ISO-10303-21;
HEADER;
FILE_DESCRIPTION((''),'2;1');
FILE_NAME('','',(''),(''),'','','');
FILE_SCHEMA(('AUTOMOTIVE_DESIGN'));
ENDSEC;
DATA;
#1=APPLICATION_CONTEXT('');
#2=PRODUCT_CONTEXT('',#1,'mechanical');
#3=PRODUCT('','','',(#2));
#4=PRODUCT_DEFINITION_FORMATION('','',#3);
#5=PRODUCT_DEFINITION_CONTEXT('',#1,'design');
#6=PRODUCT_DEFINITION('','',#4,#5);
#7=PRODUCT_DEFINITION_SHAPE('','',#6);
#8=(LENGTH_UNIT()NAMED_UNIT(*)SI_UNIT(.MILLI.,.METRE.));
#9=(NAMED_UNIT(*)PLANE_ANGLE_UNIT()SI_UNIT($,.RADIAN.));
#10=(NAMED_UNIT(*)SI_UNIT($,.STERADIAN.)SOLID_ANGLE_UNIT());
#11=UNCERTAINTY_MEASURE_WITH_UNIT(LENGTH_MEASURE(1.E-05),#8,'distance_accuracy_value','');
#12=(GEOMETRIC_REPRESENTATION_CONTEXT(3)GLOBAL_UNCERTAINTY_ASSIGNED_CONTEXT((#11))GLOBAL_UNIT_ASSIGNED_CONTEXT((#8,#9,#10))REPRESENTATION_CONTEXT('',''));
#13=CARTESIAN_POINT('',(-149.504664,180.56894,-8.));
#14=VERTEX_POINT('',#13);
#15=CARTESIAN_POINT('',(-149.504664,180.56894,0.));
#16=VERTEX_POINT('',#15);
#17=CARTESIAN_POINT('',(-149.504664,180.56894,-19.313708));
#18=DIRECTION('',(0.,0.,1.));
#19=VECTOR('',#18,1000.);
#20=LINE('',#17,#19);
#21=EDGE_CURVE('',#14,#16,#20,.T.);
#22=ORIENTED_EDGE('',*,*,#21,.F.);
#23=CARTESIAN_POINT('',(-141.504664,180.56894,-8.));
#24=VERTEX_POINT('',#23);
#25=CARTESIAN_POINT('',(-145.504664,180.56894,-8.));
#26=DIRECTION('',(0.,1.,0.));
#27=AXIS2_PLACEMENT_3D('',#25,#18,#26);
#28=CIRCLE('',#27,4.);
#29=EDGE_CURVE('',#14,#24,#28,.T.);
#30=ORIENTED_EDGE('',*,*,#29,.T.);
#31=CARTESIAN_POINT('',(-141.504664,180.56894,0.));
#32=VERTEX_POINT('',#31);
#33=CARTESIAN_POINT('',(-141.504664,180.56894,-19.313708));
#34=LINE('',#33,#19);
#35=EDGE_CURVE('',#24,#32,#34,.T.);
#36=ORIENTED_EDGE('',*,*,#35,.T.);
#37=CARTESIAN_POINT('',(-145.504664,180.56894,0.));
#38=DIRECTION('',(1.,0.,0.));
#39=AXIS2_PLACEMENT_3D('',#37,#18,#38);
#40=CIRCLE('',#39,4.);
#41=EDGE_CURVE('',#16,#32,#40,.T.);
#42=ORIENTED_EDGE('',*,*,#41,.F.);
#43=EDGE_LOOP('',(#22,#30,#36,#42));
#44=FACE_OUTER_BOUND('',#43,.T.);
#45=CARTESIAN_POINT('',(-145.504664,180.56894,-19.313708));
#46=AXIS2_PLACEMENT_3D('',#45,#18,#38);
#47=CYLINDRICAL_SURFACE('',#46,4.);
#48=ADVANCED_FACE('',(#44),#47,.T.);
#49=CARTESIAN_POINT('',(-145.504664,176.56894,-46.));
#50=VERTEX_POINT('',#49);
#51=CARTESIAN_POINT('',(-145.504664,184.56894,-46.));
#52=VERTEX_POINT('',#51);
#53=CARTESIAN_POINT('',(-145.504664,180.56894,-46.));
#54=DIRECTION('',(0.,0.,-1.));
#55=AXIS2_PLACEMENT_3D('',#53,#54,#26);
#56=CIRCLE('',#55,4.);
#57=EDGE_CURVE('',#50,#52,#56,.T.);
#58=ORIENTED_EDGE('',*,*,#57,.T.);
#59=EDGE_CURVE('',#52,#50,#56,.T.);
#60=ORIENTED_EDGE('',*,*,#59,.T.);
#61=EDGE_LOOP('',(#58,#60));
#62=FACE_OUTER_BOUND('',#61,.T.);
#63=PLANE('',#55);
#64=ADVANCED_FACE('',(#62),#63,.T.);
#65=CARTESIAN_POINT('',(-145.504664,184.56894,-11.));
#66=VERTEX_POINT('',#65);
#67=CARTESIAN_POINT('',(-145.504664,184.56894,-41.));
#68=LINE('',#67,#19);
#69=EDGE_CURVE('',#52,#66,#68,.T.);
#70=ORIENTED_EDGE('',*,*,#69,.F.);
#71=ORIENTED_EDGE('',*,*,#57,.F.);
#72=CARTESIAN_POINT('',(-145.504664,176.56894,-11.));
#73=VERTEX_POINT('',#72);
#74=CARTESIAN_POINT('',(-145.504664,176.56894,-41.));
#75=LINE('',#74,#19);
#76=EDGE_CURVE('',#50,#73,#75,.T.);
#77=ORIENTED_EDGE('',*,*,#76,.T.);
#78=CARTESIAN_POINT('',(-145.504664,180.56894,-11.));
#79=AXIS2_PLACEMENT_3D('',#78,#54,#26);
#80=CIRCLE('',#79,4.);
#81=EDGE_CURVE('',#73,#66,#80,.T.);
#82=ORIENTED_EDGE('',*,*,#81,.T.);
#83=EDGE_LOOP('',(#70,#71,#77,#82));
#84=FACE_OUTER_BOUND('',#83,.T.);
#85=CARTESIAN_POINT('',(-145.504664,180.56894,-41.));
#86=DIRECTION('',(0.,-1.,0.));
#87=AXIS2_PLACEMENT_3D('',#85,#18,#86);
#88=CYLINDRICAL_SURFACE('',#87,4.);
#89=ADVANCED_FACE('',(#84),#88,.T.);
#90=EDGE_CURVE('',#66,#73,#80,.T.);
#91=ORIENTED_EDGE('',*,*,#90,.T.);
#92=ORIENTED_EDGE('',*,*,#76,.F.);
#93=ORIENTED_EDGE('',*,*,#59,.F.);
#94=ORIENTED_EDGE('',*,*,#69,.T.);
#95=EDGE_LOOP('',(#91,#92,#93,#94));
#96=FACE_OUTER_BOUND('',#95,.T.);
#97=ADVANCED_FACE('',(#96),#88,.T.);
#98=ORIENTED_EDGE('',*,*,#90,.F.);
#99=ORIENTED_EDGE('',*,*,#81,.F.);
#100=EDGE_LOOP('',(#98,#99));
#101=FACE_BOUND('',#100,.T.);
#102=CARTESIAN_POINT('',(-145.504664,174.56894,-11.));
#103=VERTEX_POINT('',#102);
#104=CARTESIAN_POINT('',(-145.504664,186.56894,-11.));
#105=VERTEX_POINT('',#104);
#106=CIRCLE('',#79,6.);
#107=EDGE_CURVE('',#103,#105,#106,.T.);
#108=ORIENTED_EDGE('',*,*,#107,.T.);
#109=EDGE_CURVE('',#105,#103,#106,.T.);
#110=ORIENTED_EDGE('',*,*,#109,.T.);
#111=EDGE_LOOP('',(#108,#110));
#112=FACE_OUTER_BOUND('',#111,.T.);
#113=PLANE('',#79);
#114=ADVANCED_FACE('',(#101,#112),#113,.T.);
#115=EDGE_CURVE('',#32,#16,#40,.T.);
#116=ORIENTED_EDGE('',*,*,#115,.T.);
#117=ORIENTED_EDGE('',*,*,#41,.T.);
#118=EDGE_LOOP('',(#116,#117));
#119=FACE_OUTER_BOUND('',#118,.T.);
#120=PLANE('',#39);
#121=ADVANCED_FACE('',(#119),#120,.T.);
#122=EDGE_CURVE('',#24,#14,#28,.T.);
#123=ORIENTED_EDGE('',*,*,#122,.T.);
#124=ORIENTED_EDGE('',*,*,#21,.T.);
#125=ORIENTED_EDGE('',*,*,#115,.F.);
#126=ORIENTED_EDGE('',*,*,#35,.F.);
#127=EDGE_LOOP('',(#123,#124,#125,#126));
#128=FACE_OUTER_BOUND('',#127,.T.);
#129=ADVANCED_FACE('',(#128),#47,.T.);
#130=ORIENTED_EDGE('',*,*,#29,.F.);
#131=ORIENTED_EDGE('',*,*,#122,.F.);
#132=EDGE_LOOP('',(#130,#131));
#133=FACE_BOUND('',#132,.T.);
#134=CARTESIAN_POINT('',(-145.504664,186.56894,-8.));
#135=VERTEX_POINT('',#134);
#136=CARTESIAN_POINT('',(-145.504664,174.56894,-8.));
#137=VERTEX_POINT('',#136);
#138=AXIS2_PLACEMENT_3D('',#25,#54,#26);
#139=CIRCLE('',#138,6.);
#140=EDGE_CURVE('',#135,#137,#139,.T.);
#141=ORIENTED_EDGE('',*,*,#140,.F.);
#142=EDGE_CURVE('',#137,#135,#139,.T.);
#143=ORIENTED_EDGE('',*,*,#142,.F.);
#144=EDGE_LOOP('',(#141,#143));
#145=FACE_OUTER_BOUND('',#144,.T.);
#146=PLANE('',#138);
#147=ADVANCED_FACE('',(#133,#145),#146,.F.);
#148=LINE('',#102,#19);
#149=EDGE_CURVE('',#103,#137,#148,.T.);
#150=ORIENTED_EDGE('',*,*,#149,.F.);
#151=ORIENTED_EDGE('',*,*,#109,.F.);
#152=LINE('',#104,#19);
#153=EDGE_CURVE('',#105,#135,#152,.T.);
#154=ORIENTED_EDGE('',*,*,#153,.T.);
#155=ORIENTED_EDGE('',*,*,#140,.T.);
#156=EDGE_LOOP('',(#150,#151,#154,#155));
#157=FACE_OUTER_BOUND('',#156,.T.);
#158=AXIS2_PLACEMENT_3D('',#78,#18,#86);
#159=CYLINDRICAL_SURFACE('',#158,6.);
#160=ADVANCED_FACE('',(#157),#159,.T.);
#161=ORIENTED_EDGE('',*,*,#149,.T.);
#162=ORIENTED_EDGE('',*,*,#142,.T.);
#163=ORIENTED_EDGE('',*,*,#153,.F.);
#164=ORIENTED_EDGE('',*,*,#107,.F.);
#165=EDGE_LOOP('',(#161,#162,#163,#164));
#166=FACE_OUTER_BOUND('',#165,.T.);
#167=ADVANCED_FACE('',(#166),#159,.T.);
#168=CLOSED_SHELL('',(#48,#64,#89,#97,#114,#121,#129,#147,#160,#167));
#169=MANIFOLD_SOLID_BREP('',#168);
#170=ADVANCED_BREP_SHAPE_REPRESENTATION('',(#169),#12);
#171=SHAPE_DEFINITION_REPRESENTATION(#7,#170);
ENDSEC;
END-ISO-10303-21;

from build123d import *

# Parameters (mm, degrees)
SKETCH_1_R      = 4
EXTRUDE_1_DEPTH = 8
SKETCH_2_R      = 6
EXTRUDE_2_DEPTH = 3
SKETCH_3_R      = 4
EXTRUDE_3_DEPTH = 30
SKETCH_4_R      = 4
EXTRUDE_4_DEPTH = 5


with BuildPart() as part:
    # 草图1 → 凸台-拉伸1 (new body)
    with BuildSketch(Plane.XY):
        with Locations((-145.504664302, 180.568940096)):
            Circle(SKETCH_1_R)
    extrude(amount=-EXTRUDE_1_DEPTH)

    # 草图2 → 凸台-拉伸2 (add)
    with BuildSketch(Plane(origin=(0, 0, -8), x_dir=(-1, 0, 0), z_dir=(0, 0, -1))):
        with Locations(Location((145.504664302, 180.568940096, 0), (0, 0, 90))):
            Circle(SKETCH_2_R)
    extrude(amount=EXTRUDE_2_DEPTH)

    # 草图3 → 凸台-拉伸3 (add)
    with BuildSketch(Plane(origin=(0, 0, -11), x_dir=(-1, 0, 0), z_dir=(0, 0, -1))):
        with Locations(Location((145.504664302, 180.568940096, 0), (0, 0, 180))):
            Circle(SKETCH_3_R)
    extrude(amount=EXTRUDE_3_DEPTH)

    # 草图4 → 凸台-拉伸4 (add)
    with BuildSketch(Plane(origin=(0, 0, -41), x_dir=(-1, 0, 0), z_dir=(0, 0, -1))):
        with Locations(Location((145.504664302, 180.568940096, 0), (0, 0, 180))):
            Circle(SKETCH_4_R)
    extrude(amount=EXTRUDE_4_DEPTH)


solid = part.part
